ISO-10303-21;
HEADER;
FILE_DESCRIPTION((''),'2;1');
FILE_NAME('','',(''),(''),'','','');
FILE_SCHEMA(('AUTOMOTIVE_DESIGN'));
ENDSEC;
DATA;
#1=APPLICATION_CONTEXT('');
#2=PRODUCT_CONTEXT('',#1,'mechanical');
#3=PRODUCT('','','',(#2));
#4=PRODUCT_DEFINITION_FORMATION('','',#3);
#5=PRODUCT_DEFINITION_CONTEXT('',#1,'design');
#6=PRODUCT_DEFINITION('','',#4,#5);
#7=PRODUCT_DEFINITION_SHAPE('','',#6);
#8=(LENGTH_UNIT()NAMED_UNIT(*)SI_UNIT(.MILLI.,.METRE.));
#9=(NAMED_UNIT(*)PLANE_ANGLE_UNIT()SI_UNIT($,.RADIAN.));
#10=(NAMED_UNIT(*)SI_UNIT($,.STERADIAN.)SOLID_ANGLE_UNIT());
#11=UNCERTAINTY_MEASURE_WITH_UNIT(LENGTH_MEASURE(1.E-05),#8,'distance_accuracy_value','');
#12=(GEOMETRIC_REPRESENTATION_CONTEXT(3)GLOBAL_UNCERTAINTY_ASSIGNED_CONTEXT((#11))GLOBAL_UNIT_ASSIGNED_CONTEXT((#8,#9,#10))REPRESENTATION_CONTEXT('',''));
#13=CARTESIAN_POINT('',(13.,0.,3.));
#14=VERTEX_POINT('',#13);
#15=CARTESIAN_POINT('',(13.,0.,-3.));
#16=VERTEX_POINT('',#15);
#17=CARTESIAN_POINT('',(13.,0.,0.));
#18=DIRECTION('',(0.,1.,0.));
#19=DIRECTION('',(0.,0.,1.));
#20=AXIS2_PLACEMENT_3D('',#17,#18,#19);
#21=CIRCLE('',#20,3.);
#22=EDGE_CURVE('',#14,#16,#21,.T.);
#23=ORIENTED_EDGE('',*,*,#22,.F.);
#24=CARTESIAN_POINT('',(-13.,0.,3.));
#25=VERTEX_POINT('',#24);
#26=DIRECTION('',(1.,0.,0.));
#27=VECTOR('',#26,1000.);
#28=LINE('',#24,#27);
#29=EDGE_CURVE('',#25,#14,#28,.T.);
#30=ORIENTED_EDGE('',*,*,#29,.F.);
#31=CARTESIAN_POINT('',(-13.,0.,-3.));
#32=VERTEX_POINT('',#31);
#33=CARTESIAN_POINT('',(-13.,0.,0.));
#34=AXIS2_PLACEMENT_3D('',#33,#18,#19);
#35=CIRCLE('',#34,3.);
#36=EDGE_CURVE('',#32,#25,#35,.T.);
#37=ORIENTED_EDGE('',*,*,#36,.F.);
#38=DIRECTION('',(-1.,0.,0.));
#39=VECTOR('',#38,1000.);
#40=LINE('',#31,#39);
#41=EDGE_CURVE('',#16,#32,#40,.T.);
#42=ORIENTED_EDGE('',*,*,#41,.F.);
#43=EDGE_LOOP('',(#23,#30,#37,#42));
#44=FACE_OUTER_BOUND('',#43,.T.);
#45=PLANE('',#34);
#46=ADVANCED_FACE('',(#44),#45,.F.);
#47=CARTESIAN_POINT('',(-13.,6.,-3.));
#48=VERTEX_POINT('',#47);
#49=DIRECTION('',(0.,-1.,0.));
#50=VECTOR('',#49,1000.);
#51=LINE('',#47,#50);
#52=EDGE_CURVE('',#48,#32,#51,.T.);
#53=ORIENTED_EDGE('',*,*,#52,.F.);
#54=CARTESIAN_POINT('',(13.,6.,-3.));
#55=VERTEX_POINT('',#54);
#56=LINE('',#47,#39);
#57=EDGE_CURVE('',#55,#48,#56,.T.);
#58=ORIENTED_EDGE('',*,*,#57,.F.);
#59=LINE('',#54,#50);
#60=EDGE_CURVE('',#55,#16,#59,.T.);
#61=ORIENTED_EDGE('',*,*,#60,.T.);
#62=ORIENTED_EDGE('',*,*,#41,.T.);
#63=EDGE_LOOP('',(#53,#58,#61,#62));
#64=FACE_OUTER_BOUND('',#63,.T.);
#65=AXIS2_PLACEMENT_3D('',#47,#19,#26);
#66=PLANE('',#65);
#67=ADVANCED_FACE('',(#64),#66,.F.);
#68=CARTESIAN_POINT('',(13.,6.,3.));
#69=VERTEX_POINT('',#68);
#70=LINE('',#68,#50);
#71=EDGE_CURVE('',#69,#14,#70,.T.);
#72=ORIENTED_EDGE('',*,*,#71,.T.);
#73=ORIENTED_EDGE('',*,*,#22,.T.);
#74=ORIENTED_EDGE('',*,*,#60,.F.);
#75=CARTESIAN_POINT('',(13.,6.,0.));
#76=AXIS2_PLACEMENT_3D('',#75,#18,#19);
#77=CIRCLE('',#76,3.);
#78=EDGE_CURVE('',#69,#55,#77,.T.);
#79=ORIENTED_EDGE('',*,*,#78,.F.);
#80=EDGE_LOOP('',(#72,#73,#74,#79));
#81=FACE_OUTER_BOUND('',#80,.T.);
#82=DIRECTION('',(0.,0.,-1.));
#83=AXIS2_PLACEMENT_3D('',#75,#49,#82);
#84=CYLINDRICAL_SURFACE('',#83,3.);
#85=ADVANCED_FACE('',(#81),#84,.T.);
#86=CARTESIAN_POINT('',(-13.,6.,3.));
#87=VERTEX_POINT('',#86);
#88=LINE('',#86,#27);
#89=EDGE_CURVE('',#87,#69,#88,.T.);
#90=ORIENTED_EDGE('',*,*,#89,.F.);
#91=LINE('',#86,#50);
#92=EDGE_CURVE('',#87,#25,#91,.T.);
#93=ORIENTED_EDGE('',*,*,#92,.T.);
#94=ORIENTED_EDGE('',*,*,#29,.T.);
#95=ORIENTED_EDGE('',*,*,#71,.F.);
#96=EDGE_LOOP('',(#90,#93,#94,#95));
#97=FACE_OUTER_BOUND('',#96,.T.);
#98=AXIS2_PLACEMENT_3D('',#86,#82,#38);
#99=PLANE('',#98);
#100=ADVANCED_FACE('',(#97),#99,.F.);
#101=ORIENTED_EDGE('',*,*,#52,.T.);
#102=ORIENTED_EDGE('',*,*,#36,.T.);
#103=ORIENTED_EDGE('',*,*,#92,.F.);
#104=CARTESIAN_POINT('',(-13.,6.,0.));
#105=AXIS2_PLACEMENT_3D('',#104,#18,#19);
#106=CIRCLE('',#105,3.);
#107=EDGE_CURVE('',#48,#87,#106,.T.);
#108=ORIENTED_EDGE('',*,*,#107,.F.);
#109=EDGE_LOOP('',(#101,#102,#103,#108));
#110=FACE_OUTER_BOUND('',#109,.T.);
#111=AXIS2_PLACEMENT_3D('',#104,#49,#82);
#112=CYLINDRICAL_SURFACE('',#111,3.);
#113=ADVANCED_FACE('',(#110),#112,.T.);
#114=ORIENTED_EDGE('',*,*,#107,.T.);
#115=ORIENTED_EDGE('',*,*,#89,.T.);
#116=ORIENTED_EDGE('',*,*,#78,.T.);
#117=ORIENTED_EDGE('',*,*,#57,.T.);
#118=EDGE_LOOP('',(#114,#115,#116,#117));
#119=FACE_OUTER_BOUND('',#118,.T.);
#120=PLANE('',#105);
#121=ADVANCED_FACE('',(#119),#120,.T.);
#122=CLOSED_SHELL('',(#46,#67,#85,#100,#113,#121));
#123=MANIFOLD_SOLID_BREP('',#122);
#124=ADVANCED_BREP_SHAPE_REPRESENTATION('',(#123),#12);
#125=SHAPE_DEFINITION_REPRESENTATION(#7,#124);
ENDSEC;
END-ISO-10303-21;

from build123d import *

# Parameters (mm, degrees)
KEY_BODY_6X6X32_DEPTH = 6


with BuildPart() as part:
    # Key Profile Slot 6x32 → Key Body 6x6x32 (new body)
    with BuildSketch(Plane(origin=(0, 0, 0), x_dir=(1, 0, 0), z_dir=(0, 1, 0))):
        with BuildLine():
            Line((-13, 3), (13, 3))
            ThreePointArc((13, 3), (16, 0), (13, -3))
            Line((13, -3), (-13, -3))
            ThreePointArc((-13, -3), (-16, 0), (-13, 3))
        make_face()
    extrude(amount=KEY_BODY_6X6X32_DEPTH)


solid = part.part
